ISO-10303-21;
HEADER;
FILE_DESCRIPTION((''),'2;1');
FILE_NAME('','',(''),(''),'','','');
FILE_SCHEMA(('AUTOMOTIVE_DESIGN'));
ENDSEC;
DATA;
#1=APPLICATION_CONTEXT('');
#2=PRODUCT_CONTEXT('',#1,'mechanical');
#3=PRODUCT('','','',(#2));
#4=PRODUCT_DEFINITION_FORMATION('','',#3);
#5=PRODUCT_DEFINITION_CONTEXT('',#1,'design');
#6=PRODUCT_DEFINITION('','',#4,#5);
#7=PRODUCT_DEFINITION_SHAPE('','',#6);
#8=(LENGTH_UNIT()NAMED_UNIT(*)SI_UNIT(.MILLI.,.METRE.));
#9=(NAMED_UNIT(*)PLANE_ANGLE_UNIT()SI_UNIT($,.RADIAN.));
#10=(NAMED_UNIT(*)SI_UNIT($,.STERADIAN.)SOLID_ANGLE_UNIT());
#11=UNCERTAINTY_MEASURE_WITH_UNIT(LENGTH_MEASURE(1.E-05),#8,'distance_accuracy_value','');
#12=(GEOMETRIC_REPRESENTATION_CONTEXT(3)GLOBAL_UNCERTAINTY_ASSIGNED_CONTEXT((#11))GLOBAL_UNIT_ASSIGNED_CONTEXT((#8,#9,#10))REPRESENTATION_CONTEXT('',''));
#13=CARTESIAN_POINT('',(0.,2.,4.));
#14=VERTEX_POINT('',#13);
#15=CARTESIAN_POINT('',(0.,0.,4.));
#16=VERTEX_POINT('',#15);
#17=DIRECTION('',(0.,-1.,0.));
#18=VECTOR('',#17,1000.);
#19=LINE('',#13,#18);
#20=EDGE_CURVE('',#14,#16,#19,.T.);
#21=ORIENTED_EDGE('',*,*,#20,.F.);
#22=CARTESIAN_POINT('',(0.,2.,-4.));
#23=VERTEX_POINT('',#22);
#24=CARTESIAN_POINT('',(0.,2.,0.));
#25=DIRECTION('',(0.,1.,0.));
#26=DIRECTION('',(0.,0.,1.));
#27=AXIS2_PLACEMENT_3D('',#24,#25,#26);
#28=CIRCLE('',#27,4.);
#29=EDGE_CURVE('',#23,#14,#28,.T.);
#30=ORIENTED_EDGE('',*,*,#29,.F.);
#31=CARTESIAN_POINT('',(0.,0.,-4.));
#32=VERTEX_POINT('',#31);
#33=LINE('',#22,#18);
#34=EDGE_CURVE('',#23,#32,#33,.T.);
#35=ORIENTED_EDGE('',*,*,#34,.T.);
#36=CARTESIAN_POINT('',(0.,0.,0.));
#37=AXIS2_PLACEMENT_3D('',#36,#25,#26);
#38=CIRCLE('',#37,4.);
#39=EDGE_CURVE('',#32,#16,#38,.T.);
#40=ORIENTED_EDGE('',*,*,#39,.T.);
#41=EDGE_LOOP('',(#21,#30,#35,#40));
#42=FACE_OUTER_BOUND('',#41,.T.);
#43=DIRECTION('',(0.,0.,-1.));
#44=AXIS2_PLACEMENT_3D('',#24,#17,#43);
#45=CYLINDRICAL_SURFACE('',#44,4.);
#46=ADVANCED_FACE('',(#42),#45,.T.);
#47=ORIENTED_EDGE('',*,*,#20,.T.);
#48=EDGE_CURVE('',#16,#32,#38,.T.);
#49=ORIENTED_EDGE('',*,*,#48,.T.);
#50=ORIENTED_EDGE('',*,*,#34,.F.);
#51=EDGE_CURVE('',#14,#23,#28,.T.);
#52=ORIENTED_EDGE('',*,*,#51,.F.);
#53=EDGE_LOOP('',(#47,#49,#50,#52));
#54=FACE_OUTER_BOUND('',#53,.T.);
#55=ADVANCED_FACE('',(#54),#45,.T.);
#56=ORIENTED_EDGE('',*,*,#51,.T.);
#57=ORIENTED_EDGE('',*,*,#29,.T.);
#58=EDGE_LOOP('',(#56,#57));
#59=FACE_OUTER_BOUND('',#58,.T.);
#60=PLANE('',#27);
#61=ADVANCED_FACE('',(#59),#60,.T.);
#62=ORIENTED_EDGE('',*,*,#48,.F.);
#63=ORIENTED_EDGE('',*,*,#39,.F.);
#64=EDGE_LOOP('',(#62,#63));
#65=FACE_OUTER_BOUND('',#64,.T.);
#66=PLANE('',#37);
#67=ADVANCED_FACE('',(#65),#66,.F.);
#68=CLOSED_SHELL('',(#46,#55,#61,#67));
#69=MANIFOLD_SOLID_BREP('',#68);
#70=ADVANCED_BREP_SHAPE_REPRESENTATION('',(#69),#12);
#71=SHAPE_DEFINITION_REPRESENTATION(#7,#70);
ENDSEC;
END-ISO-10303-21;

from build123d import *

# Parameters (mm, degrees)
SKETCH1_R           = 4
BOSS_EXTRUDE1_DEPTH = 2


with BuildPart() as part:
    # Sketch1 → Boss-Extrude1 (new body)
    with BuildSketch(Plane(origin=(0, 0, 0), x_dir=(1, 0, 0), z_dir=(0, 1, 0))):
        with Locations(Location((0, 0, 0), (0, 0, 270))):
            Circle(SKETCH1_R)
    extrude(amount=BOSS_EXTRUDE1_DEPTH)


solid = part.part
